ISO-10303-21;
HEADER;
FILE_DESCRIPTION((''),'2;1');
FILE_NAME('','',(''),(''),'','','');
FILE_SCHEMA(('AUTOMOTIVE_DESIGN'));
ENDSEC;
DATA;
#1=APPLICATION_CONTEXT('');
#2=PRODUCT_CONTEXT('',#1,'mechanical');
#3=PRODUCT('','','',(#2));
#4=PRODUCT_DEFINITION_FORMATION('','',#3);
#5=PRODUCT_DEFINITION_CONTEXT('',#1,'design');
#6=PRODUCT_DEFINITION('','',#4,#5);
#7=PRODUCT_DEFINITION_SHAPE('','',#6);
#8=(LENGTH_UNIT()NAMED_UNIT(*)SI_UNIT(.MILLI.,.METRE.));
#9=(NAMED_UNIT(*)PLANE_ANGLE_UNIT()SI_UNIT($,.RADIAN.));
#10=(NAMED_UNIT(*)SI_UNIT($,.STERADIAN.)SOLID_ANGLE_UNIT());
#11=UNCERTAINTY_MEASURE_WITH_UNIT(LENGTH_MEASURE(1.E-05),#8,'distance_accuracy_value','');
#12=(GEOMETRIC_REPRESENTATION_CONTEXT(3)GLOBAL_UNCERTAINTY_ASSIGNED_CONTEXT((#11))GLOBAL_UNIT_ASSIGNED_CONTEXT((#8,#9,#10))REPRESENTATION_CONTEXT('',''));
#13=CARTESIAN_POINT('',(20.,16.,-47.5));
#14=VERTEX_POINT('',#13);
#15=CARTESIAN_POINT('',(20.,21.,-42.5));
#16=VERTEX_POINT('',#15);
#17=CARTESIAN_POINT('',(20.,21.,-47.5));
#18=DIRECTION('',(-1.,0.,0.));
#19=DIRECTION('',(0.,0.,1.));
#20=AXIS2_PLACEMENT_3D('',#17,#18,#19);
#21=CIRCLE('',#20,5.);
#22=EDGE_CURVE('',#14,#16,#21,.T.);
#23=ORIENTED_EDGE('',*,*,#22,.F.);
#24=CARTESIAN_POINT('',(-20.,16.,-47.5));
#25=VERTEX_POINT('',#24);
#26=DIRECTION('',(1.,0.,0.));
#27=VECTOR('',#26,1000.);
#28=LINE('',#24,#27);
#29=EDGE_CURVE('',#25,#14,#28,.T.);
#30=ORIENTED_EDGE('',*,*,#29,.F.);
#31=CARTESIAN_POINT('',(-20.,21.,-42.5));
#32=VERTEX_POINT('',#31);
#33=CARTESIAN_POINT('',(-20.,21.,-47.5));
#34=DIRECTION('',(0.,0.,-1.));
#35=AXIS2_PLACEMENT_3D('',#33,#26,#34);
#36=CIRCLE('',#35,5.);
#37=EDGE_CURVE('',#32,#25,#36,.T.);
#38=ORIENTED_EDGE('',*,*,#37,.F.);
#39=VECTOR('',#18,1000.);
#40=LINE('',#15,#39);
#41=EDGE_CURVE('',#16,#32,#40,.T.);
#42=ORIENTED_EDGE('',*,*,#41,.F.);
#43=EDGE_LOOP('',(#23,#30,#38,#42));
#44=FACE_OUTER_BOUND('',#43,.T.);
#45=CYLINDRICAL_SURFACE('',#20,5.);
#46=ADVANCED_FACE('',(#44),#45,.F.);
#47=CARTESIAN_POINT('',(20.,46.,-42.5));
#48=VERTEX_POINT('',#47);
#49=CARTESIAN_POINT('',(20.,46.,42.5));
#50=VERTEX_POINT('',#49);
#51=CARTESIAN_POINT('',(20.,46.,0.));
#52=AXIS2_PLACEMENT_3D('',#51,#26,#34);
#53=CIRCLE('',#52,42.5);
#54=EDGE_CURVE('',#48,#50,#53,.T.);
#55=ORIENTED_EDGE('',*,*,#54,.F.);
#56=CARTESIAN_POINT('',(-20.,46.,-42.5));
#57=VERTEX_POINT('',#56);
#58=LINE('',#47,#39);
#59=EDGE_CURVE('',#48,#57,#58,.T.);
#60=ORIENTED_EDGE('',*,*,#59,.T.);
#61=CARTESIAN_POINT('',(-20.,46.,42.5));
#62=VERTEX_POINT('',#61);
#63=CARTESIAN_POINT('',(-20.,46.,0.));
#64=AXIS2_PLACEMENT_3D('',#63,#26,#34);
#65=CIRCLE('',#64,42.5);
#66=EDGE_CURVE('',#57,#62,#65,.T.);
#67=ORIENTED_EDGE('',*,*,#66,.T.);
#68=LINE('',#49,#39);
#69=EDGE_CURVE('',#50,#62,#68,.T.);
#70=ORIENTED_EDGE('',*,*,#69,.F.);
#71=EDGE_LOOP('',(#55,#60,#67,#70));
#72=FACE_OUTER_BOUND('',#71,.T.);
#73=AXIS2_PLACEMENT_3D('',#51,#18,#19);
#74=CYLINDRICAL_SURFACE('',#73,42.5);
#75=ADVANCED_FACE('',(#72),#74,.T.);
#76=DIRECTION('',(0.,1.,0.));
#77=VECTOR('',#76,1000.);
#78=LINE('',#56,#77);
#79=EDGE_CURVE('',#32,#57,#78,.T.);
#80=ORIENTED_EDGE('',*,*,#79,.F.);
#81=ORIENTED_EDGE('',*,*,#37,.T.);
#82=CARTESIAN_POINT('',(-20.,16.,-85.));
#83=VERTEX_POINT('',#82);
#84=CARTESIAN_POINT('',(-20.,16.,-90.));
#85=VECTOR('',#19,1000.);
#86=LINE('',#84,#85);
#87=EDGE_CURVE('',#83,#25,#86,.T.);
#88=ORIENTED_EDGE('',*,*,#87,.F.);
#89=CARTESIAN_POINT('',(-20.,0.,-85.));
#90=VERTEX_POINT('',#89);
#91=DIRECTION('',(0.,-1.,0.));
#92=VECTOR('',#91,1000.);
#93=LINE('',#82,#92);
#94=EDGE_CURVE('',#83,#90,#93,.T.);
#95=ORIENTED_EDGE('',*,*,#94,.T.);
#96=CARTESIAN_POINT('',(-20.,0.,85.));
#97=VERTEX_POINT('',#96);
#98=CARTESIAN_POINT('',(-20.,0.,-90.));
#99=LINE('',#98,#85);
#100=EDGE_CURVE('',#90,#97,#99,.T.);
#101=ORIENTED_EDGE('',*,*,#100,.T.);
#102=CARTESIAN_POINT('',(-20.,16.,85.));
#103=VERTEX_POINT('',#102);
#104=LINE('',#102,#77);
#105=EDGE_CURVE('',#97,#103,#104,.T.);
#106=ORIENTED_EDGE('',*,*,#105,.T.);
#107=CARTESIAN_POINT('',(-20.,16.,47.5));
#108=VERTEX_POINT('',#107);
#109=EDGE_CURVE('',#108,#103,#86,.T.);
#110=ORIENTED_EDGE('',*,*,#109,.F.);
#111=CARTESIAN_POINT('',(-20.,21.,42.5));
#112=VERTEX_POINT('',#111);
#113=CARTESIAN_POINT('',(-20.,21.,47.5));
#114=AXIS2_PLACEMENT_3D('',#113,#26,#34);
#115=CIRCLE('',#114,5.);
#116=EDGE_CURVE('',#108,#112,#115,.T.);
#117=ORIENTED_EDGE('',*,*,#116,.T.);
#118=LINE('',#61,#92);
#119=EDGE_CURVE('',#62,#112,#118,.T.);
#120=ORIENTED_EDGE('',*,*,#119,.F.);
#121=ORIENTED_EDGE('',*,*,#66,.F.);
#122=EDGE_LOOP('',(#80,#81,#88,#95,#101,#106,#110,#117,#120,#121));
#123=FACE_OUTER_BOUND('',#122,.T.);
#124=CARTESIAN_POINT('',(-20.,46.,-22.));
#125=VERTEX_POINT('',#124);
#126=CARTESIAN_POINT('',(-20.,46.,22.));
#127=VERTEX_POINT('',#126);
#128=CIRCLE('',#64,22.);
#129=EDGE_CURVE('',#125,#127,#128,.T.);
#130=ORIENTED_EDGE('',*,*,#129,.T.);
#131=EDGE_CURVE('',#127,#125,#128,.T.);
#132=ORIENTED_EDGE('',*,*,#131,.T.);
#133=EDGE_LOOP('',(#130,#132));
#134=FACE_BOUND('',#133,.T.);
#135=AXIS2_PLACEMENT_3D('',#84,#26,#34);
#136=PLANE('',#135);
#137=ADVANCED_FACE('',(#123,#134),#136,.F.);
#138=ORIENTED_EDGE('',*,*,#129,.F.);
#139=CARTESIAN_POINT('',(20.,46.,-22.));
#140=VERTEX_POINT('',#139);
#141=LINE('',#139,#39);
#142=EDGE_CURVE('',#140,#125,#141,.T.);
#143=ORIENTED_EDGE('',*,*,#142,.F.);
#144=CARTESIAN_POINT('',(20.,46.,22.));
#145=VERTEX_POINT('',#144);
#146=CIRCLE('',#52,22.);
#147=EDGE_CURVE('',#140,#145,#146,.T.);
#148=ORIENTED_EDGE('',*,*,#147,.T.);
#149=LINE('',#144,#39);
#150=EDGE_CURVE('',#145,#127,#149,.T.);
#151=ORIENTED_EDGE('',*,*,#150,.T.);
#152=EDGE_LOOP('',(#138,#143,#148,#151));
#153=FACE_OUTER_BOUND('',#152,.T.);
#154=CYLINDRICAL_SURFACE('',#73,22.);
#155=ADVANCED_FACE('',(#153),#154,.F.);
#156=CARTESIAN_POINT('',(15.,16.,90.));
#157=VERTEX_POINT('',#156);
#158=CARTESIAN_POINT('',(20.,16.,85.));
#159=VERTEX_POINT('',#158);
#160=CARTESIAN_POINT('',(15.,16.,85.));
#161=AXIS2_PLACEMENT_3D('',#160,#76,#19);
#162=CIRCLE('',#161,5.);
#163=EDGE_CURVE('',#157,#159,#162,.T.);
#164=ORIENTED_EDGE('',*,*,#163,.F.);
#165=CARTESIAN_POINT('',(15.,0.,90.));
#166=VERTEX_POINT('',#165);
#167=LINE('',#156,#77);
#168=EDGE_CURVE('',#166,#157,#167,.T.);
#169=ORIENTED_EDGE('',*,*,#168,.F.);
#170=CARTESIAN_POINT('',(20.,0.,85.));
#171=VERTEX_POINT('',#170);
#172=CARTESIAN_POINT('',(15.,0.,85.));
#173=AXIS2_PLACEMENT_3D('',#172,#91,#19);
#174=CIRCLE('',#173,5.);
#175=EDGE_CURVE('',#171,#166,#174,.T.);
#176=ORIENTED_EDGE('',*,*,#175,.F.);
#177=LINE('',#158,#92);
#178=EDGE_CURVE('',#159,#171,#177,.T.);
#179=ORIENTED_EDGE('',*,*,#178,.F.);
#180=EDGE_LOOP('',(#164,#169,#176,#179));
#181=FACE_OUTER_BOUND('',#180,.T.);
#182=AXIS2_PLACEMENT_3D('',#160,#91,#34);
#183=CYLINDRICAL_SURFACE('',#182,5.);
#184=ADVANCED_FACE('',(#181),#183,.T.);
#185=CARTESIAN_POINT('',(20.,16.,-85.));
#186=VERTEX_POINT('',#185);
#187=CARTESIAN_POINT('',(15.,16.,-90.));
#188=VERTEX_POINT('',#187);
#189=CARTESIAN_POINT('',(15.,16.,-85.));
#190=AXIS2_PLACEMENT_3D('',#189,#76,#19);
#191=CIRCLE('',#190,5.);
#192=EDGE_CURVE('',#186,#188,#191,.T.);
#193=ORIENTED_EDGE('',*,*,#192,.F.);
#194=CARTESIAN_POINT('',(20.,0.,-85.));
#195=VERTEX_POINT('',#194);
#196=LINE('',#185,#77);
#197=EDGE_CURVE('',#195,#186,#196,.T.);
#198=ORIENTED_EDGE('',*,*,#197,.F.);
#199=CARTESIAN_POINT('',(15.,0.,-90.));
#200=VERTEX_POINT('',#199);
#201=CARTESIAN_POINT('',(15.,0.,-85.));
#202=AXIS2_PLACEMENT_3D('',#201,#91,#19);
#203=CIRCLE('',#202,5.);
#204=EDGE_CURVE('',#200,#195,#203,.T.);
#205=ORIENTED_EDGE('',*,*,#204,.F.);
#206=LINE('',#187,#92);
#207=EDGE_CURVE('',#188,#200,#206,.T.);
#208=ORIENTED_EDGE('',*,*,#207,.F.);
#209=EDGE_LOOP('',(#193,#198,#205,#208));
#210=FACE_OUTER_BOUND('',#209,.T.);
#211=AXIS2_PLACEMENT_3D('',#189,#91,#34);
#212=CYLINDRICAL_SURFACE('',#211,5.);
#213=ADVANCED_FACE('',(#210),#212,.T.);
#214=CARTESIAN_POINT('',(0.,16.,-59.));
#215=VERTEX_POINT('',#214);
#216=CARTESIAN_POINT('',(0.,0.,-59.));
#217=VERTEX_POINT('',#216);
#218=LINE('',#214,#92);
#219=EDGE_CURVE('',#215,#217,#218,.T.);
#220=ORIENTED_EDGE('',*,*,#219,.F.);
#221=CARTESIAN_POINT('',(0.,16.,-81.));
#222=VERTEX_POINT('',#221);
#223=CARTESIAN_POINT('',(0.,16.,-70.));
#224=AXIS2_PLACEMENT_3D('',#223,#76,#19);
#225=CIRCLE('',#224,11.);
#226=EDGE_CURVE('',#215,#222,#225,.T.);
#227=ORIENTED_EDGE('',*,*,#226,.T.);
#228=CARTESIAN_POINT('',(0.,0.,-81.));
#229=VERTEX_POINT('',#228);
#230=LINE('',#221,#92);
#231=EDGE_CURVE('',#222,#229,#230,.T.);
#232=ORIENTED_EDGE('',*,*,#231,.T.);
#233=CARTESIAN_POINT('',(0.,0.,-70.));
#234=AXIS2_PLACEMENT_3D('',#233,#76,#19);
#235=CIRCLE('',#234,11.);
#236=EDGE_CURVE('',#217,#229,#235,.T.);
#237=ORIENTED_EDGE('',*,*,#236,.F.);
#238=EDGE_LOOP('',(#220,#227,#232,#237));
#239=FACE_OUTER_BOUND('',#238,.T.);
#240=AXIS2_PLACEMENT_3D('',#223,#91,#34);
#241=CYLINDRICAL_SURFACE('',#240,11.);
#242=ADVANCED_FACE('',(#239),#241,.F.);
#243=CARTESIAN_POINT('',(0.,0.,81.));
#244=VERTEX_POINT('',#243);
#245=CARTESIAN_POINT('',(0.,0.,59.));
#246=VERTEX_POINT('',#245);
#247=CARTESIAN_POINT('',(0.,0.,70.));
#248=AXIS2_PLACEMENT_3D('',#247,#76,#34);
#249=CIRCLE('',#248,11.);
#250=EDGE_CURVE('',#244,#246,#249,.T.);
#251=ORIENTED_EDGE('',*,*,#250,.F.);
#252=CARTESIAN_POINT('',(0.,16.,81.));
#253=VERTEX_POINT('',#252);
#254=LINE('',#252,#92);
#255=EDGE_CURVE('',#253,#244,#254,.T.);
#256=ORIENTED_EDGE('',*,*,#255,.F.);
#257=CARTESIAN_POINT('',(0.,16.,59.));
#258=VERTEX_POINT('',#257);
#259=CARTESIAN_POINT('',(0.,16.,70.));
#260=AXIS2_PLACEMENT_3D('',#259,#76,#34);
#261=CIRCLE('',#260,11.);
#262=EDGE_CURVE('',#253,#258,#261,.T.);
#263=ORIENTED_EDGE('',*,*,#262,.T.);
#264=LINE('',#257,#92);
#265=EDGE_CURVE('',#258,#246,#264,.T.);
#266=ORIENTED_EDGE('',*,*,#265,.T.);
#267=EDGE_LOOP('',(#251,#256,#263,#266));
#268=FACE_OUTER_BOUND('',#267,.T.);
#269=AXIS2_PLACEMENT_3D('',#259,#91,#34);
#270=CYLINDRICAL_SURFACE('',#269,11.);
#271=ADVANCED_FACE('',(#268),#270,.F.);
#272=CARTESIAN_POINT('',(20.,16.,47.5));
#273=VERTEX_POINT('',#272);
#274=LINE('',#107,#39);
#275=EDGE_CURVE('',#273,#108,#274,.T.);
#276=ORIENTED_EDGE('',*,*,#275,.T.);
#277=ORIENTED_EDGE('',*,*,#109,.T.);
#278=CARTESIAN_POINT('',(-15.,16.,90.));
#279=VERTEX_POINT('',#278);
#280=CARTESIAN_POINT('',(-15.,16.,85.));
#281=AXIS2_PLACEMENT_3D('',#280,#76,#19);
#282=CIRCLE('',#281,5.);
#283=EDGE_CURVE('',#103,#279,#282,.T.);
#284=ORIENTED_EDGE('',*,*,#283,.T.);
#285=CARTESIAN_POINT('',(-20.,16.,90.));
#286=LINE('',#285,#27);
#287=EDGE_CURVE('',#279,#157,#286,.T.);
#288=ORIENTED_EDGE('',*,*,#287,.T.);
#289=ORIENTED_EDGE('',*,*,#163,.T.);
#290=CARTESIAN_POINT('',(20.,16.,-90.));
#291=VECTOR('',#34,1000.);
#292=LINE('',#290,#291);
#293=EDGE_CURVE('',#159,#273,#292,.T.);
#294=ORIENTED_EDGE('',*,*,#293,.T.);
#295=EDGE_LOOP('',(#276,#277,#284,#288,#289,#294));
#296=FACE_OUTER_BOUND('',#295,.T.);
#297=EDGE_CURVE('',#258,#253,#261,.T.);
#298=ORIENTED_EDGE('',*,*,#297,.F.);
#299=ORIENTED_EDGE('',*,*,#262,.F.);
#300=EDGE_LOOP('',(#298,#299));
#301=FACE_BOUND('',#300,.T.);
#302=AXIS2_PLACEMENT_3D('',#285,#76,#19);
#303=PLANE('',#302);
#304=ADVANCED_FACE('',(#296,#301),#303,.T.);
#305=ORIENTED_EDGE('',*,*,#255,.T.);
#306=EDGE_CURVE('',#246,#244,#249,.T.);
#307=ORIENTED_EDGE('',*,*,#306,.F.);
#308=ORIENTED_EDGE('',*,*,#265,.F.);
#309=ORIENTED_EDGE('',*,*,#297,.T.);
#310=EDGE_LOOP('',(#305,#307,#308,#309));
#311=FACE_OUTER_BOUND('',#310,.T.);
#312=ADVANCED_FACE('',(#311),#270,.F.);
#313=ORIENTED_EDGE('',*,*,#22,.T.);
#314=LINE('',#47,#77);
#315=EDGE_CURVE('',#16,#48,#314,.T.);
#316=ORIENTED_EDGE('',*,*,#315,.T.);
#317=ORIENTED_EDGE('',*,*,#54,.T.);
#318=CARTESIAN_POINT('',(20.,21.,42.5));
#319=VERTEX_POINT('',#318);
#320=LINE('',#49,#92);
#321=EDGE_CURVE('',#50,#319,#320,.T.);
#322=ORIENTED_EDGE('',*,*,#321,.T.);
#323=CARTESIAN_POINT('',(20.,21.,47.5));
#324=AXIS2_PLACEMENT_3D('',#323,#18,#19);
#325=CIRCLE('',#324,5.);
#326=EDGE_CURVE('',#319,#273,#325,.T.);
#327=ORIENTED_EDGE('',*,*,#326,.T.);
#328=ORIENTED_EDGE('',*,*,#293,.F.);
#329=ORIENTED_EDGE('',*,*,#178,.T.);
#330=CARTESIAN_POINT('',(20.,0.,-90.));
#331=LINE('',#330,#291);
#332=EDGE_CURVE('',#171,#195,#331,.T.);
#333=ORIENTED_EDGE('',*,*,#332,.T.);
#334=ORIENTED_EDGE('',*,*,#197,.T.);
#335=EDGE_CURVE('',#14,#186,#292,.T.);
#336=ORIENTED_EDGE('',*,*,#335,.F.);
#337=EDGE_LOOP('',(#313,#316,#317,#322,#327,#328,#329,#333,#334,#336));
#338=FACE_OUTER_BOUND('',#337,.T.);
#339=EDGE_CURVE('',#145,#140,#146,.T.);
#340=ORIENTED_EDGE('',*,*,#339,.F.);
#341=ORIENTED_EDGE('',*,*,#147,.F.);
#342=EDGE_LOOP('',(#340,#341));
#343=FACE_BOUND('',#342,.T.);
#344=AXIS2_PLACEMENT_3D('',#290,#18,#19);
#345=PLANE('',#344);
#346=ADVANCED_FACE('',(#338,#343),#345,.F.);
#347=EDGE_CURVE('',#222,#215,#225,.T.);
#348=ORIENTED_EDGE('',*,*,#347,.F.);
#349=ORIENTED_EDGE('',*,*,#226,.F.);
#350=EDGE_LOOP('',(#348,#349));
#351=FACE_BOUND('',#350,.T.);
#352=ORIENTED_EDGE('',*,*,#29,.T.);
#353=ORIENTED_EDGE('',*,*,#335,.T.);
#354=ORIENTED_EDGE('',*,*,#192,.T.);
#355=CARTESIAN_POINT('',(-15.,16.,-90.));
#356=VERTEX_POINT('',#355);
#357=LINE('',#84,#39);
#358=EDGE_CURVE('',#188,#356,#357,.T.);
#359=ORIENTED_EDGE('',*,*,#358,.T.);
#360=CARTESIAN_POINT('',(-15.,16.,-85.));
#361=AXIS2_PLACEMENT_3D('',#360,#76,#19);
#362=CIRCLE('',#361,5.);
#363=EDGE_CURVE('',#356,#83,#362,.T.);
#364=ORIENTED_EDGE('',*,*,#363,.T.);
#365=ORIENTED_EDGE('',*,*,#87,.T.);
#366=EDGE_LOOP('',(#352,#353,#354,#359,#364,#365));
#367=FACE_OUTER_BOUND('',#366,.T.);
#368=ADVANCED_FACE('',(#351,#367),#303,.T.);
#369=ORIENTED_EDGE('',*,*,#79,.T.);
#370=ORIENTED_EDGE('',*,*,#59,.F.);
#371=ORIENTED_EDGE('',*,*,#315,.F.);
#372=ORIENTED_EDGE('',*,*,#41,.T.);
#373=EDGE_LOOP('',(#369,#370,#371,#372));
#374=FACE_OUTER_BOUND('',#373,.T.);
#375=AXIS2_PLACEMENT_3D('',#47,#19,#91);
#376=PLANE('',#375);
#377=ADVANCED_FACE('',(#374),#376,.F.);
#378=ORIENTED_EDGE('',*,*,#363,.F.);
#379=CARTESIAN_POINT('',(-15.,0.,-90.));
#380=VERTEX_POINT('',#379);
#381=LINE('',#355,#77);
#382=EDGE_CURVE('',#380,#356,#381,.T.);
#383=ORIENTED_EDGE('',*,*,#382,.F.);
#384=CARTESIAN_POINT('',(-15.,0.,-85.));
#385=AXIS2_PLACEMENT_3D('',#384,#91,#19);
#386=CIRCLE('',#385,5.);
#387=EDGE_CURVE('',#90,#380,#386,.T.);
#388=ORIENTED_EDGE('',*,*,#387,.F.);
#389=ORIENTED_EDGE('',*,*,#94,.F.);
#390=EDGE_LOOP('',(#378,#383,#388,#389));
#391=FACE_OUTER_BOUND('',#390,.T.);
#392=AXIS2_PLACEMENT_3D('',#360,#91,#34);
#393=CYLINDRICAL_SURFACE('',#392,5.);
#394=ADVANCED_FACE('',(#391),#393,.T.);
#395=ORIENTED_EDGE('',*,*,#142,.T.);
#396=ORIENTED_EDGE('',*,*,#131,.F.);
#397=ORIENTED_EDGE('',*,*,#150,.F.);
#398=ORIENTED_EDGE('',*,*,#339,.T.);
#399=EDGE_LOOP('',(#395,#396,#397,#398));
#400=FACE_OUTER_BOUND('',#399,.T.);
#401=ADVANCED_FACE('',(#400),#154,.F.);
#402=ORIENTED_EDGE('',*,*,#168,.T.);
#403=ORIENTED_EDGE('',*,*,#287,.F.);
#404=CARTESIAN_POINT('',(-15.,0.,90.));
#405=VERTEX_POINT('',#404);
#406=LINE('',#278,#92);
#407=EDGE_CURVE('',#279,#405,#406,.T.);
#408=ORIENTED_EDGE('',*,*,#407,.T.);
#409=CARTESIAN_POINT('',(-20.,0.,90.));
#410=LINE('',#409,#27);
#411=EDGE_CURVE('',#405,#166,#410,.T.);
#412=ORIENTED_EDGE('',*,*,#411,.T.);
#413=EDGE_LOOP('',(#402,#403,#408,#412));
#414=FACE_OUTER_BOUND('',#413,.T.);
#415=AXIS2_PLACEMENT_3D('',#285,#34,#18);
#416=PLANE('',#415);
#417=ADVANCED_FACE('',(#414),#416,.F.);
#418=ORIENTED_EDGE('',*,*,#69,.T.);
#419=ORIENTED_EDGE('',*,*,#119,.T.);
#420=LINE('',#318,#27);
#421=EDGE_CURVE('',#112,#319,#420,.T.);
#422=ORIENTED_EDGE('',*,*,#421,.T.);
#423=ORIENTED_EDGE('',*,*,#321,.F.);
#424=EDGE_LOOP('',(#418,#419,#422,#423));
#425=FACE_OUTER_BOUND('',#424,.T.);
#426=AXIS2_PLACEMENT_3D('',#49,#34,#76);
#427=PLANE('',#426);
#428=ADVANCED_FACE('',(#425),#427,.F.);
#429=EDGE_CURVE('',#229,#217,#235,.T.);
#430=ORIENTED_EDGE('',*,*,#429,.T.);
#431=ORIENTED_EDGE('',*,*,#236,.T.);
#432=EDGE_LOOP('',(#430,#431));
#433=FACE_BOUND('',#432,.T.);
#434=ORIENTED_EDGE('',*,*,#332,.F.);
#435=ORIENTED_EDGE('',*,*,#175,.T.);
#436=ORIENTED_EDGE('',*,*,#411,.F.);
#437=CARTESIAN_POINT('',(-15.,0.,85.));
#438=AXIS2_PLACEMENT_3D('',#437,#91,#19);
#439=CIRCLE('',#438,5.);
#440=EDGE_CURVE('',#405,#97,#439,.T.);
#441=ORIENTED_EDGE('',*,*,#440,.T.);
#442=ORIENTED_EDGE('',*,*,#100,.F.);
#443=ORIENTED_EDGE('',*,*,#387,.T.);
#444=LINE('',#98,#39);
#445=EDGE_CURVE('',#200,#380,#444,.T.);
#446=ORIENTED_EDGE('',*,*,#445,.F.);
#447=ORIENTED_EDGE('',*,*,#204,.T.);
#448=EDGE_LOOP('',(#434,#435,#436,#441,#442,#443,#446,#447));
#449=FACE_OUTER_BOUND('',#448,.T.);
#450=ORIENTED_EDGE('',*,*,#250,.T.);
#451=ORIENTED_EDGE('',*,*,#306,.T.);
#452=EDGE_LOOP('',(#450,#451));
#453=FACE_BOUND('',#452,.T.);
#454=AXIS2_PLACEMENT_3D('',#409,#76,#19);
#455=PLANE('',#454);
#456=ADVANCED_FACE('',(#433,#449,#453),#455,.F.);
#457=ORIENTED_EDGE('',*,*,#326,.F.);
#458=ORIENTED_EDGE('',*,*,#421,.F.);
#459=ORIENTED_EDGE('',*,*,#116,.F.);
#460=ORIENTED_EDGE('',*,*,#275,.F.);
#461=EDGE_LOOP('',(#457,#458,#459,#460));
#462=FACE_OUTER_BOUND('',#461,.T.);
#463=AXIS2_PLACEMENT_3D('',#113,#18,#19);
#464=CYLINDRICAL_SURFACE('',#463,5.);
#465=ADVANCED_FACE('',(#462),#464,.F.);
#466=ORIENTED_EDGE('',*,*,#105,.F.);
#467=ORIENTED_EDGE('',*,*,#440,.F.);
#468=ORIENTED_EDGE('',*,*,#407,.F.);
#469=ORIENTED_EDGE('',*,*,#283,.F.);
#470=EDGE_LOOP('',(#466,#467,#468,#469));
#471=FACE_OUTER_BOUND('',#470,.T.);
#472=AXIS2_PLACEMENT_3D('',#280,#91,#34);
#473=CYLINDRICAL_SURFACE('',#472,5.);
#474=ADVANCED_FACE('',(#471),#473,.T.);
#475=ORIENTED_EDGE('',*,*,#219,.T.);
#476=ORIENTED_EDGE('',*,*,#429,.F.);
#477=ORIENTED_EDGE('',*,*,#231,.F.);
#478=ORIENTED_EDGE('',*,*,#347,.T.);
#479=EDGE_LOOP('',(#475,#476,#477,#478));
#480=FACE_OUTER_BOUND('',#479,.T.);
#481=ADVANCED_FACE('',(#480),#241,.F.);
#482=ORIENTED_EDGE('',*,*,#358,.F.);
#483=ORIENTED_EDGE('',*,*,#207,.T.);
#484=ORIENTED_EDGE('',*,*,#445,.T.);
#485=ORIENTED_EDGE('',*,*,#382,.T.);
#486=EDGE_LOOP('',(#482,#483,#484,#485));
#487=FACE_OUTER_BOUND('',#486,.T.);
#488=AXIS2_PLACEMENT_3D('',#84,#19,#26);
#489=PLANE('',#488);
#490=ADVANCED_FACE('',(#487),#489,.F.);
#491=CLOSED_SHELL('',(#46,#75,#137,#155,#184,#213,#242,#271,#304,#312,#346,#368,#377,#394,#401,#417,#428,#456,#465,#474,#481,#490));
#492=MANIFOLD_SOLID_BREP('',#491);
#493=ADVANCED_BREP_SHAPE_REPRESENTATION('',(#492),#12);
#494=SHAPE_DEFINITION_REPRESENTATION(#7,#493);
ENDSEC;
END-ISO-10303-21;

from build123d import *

# Parameters (mm, degrees)
SKETCH1_W           = 40
SKETCH1_H           = 180
SKETCH1_R           = 11
BOSS_EXTRUDE1_DEPTH = 16
SKETCH2_R           = 22
BOSS_EXTRUDE2_DEPTH = 20
FILLET1_R           = 5


with BuildPart() as part:
    # Sketch1 → Boss-Extrude1 (new body)
    with BuildSketch(Plane(origin=(0, 0, 0), x_dir=(1, 0, 0), z_dir=(0, 1, 0))):
        Rectangle(SKETCH1_W, SKETCH1_H)
        with Locations(Location((0, 70, 0), (0, 0, 270))):
            Circle(SKETCH1_R, mode=Mode.SUBTRACT)
        with Locations(Location((0, -70, 0), (0, 0, 90))):
            Circle(SKETCH1_R, mode=Mode.SUBTRACT)
    extrude(amount=BOSS_EXTRUDE1_DEPTH)

    # Sketch2 → Boss-Extrude2 (add, symmetric)
    with BuildSketch(Plane(origin=(0, 0, 0), x_dir=(0, 0, -1), z_dir=(1, 0, 0))):
        with BuildLine():
            Line((-42.5, 46), (-42.5, 16))
            Line((-42.5, 16), (42.5, 16))
            Line((42.5, 16), (42.5, 46))
            ThreePointArc((42.5, 46), (0, 88.5), (-42.5, 46))
        make_face()
        with Locations((0, 46)):
            Circle(SKETCH2_R, mode=Mode.SUBTRACT)
    extrude(amount=BOSS_EXTRUDE2_DEPTH, both=True)

    # Fillet1
    fillet1_edges = [part.edges().sort_by_distance(p)[0] for p in [
        (0, 16, 42.5),
        (20, 8, 90),
        (-20, 8, 90),
        (20, 8, -90),
        (-20, 8, -90),
        (0, 16, -42.5),
    ]]
    fillet(fillet1_edges, radius=FILLET1_R)


solid = part.part
